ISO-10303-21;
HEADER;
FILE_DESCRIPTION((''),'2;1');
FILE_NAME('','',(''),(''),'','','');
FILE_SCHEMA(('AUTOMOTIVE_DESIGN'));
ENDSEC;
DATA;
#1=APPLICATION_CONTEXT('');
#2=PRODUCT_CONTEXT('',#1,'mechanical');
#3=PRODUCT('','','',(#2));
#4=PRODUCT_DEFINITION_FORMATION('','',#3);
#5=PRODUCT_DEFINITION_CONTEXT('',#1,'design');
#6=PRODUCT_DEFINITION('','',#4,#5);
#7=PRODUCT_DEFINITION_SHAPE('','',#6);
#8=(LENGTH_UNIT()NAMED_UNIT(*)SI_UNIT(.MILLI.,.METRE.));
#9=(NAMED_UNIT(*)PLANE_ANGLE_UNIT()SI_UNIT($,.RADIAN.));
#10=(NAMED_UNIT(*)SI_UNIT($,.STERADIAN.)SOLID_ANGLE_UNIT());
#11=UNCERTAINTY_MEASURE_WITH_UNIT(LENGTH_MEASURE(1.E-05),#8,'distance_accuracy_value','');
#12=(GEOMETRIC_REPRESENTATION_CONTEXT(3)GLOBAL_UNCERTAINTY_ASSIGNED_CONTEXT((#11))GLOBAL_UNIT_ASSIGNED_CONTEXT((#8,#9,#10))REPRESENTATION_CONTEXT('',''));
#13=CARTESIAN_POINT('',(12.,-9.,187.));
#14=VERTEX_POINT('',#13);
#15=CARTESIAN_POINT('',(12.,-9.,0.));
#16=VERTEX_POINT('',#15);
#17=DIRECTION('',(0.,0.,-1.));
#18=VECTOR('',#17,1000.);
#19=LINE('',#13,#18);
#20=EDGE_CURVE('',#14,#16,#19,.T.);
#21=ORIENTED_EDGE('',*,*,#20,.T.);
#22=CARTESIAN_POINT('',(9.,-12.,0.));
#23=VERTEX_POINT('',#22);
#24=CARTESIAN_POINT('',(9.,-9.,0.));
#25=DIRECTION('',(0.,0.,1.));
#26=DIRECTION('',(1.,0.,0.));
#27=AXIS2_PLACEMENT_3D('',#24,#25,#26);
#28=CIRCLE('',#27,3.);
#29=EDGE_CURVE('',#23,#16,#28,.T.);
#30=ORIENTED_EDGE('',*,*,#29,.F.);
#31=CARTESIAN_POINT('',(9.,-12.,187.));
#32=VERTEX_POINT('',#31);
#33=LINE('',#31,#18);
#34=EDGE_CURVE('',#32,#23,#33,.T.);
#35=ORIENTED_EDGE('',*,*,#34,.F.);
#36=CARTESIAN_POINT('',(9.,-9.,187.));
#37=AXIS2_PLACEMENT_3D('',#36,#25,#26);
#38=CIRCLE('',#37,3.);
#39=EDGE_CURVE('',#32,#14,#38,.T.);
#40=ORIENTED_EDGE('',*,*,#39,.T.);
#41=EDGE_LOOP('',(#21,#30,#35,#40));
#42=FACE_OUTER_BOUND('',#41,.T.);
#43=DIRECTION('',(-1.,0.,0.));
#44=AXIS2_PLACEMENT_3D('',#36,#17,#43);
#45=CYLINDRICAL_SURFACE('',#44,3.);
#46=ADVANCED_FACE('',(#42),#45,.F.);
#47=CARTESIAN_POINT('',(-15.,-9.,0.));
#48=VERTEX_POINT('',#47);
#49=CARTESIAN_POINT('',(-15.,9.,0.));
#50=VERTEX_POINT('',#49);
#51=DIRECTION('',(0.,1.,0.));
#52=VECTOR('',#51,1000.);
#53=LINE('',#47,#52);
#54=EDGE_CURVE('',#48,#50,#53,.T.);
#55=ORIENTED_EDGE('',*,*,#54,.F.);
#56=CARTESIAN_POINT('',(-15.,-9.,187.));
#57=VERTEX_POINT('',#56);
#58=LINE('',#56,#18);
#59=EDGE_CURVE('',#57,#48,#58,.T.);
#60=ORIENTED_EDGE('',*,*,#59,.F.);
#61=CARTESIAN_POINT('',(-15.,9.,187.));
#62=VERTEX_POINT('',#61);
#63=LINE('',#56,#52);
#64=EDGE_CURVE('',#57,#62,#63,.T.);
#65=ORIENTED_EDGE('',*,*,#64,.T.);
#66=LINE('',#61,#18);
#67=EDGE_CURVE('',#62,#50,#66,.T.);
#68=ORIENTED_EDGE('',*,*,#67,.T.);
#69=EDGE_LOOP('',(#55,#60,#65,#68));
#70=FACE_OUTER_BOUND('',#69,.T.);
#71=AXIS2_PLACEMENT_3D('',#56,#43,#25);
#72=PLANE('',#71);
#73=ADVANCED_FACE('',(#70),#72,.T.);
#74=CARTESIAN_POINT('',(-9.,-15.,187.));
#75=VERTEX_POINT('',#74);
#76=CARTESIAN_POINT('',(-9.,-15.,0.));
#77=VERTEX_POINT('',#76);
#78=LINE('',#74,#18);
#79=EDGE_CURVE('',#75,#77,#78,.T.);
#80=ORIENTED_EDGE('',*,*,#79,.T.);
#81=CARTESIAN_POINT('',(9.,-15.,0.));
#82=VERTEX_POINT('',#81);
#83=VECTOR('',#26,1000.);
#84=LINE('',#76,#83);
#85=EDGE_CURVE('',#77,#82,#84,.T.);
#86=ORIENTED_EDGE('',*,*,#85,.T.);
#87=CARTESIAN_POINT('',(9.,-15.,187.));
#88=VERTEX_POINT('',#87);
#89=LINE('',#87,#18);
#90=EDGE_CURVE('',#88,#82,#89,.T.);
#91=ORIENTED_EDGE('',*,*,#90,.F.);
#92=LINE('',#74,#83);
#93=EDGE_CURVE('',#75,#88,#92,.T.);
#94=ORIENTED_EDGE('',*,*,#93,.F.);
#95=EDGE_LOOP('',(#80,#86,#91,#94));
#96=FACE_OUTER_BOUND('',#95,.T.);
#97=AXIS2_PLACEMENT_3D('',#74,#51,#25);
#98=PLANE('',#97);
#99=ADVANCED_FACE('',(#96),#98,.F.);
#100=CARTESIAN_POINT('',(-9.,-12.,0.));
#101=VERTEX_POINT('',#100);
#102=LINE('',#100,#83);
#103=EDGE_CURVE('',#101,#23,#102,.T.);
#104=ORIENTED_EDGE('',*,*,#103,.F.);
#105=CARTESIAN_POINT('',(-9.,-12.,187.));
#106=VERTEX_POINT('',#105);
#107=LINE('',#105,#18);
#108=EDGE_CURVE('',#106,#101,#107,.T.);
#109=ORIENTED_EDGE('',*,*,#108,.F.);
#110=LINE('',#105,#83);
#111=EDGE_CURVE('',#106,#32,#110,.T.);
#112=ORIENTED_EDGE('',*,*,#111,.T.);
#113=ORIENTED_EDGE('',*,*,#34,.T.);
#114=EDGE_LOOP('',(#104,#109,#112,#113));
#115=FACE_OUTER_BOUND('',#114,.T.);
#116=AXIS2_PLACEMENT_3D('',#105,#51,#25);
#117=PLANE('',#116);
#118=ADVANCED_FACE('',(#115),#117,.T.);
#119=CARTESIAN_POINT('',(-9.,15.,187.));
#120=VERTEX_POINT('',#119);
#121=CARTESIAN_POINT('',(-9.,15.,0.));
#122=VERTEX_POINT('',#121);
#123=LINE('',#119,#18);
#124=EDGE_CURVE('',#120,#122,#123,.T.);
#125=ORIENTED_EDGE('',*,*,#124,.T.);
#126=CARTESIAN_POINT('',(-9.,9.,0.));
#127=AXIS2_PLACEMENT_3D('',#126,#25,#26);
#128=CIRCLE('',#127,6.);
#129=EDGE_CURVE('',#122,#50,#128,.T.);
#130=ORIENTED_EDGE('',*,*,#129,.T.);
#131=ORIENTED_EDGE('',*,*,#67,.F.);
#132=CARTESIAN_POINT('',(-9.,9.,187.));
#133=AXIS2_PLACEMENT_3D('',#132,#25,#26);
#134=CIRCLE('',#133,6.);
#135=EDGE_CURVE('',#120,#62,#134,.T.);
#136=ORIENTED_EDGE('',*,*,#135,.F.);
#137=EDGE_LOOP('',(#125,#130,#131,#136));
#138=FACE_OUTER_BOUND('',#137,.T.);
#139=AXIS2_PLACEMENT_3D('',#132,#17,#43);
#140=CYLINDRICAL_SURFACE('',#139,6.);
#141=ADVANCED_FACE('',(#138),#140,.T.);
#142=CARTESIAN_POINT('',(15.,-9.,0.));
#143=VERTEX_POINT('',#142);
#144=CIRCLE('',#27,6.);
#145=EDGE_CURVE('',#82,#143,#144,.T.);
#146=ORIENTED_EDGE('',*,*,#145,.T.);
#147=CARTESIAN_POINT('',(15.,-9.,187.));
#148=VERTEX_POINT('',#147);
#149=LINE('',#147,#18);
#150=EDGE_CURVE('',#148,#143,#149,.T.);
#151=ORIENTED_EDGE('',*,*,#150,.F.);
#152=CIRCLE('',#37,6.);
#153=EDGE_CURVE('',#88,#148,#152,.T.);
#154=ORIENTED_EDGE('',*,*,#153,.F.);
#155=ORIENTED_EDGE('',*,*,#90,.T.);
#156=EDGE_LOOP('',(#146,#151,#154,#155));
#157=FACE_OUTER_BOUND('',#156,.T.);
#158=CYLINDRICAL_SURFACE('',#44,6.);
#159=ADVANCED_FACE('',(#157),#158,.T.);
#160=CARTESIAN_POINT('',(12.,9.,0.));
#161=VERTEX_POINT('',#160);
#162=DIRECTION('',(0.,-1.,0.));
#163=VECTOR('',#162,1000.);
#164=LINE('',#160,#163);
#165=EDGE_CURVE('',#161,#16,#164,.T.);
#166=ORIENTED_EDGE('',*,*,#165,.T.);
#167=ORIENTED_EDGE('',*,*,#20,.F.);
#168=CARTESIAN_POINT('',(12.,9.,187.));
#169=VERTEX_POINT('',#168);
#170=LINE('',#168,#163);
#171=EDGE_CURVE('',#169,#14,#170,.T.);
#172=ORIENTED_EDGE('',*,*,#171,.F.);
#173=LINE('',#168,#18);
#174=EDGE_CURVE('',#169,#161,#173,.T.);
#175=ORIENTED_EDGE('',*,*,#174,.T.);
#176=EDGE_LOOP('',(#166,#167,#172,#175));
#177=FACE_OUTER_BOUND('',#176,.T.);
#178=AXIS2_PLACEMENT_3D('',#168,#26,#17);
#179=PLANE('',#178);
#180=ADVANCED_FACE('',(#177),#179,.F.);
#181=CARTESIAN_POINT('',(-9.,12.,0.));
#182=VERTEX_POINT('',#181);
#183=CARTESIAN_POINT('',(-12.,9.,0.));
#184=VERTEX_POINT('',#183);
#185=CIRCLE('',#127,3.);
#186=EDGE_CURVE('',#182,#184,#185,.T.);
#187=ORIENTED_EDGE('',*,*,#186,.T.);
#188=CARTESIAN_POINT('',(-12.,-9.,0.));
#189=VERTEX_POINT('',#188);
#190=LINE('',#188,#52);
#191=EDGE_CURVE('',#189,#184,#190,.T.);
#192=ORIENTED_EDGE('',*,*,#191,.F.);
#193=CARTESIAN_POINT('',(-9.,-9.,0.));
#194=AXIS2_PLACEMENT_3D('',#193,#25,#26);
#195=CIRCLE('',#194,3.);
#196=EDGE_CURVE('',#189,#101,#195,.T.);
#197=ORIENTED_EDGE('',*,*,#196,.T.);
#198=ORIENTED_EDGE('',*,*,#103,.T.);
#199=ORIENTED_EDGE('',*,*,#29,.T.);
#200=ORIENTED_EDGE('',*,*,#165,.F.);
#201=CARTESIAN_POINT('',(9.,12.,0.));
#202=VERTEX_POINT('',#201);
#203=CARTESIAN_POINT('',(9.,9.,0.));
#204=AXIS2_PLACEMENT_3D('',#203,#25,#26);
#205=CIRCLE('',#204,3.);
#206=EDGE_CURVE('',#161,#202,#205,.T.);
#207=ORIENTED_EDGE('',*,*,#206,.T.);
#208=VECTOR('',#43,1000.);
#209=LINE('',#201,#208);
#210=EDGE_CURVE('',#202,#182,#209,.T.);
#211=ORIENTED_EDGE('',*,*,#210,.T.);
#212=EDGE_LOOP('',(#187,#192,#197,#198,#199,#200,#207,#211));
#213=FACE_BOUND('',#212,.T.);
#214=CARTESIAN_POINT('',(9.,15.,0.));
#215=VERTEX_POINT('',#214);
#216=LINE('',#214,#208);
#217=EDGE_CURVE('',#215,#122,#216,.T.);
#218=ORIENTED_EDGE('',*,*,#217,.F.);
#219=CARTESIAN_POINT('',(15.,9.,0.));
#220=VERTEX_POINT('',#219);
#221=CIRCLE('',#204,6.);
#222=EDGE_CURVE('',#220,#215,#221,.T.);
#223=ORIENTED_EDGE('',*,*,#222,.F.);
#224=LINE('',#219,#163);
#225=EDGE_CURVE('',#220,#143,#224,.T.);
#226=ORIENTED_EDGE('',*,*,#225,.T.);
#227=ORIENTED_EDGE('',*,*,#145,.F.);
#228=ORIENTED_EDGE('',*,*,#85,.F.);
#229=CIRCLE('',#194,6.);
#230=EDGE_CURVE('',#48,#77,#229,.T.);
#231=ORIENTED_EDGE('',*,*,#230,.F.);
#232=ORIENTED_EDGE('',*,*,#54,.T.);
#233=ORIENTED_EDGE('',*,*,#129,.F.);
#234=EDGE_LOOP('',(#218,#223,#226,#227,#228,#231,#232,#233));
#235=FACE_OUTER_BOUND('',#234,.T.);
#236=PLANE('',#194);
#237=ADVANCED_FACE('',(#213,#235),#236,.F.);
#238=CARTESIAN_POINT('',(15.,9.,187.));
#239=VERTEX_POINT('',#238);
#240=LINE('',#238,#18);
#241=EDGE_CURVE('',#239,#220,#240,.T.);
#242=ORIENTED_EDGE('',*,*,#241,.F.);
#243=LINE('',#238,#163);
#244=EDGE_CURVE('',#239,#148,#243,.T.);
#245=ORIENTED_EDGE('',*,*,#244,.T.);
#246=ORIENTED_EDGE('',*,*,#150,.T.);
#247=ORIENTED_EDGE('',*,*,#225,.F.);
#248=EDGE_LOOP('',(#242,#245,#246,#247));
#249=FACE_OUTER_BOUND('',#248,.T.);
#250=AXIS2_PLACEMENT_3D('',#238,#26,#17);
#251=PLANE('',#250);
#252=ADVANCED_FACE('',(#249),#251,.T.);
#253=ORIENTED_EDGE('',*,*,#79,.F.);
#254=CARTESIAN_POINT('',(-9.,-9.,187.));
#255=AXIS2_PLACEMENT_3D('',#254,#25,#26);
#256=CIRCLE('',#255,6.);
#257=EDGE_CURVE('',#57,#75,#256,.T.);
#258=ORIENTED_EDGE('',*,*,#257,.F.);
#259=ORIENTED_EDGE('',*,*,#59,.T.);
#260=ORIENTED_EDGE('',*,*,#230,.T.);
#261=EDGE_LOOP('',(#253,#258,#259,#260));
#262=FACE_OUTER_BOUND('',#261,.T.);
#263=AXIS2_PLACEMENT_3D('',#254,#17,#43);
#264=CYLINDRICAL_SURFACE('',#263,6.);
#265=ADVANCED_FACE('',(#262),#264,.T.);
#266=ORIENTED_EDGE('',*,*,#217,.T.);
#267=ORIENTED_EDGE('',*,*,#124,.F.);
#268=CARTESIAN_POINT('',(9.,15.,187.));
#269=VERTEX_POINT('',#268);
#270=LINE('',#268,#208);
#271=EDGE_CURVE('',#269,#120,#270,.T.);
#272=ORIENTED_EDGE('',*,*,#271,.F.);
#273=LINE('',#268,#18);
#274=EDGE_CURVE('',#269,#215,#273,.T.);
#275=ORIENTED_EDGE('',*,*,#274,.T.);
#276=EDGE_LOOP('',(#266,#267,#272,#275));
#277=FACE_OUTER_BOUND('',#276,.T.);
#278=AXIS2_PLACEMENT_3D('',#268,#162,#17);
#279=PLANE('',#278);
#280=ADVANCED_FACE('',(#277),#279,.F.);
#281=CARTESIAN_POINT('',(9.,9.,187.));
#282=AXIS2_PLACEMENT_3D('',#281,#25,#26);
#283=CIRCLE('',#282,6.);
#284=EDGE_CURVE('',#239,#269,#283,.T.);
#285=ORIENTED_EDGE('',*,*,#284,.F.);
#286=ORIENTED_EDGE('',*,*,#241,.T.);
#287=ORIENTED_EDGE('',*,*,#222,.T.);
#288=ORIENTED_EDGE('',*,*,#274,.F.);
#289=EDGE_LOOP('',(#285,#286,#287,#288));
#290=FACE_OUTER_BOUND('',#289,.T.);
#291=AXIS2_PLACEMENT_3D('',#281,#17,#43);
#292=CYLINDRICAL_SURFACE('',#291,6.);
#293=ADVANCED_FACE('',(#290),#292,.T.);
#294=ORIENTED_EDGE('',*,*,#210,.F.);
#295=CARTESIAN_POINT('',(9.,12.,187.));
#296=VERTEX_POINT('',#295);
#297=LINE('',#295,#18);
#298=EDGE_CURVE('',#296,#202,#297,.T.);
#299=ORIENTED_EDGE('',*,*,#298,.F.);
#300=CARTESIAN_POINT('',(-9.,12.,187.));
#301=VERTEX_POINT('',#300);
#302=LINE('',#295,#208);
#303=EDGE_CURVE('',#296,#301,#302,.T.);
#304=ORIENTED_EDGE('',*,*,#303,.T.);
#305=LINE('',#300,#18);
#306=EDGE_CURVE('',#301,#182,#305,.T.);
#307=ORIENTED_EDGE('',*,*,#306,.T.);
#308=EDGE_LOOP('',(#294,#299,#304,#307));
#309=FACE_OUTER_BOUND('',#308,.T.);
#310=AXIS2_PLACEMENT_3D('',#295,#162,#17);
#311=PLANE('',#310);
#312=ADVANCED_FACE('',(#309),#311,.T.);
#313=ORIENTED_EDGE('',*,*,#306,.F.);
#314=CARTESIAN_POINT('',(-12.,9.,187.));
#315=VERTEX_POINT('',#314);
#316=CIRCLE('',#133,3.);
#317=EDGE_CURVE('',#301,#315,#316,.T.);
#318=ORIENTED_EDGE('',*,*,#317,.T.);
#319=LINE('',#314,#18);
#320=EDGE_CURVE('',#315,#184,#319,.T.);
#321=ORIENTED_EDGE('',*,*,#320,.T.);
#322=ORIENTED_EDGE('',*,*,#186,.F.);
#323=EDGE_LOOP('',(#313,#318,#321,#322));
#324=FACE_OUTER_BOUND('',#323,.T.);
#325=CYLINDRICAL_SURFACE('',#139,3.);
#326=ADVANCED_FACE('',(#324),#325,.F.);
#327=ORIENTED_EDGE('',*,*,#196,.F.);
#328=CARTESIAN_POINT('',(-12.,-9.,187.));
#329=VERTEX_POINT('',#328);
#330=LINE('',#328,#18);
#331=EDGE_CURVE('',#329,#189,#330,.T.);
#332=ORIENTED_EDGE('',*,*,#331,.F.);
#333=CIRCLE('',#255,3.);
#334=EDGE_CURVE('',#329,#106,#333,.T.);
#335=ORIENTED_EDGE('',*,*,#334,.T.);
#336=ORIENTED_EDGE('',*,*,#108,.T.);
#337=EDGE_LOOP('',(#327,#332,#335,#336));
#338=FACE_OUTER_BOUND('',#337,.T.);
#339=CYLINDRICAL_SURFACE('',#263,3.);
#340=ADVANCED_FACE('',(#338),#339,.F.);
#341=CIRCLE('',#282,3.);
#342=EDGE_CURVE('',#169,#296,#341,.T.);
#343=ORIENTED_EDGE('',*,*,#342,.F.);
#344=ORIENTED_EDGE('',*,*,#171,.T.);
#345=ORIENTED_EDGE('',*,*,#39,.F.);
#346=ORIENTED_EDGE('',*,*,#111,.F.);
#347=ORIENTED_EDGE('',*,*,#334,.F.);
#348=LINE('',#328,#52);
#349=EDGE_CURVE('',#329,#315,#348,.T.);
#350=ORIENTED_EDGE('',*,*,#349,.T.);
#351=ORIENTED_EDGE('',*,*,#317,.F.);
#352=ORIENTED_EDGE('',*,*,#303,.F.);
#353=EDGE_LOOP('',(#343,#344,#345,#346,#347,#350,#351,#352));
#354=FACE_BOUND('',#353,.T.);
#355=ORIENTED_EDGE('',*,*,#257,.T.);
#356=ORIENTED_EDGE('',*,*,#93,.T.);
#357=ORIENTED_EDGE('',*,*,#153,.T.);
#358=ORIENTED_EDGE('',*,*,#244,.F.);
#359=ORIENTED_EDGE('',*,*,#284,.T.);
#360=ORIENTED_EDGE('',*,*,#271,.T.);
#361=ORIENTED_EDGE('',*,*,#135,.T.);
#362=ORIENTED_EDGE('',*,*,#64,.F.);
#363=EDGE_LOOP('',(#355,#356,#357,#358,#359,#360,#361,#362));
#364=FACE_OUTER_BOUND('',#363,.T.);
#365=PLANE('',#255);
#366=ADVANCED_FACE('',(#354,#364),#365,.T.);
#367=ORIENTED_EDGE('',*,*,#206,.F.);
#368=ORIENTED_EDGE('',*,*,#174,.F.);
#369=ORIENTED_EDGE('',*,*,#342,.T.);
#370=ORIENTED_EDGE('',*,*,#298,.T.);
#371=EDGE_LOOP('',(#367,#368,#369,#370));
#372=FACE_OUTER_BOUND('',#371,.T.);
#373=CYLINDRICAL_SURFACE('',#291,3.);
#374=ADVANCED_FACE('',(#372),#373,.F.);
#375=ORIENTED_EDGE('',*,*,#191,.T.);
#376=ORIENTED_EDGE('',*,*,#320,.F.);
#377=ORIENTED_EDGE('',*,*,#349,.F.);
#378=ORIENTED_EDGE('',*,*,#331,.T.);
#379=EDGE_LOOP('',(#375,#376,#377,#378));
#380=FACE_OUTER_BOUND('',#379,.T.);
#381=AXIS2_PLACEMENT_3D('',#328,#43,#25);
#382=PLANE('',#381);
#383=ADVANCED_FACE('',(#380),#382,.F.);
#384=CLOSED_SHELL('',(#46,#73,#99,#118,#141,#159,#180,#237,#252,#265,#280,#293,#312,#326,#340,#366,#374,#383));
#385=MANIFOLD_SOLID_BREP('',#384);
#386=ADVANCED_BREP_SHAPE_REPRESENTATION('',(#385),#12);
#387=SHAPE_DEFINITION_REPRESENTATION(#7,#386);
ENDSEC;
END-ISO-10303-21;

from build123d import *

# Parameters (mm, degrees)
BOSS_EXTRUDE1_DEPTH = 187


with BuildPart() as part:
    # Sketch1 → Boss-Extrude1 (new body)
    with BuildSketch(Plane.XY):
        with BuildLine():
            Line((-9, -15), (9, -15))
            ThreePointArc((9, -15), (13.242640687, -13.242640687), (15, -9))
            Line((15, -9), (15, 9))
            ThreePointArc((15, 9), (13.242640687, 13.242640687), (9, 15))
            Line((9, 15), (-9, 15))
            ThreePointArc((-9, 15), (-13.242640687, 13.242640687), (-15, 9))
            Line((-15, 9), (-15, -9))
            ThreePointArc((-15, -9), (-13.242640687, -13.242640687), (-9, -15))
        make_face()
        with BuildLine():
            Line((-9, -12), (9, -12))
            ThreePointArc((9, -12), (11.121320344, -11.121320344), (12, -9))
            Line((12, -9), (12, 9))
            ThreePointArc((12, 9), (11.121320344, 11.121320344), (9, 12))
            Line((9, 12), (-9, 12))
            ThreePointArc((-9, 12), (-11.121320344, 11.121320344), (-12, 9))
            Line((-12, 9), (-12, -9))
            ThreePointArc((-12, -9), (-11.121320344, -11.121320344), (-9, -12))
        make_face(mode=Mode.SUBTRACT)
    extrude(amount=BOSS_EXTRUDE1_DEPTH)


solid = part.part
